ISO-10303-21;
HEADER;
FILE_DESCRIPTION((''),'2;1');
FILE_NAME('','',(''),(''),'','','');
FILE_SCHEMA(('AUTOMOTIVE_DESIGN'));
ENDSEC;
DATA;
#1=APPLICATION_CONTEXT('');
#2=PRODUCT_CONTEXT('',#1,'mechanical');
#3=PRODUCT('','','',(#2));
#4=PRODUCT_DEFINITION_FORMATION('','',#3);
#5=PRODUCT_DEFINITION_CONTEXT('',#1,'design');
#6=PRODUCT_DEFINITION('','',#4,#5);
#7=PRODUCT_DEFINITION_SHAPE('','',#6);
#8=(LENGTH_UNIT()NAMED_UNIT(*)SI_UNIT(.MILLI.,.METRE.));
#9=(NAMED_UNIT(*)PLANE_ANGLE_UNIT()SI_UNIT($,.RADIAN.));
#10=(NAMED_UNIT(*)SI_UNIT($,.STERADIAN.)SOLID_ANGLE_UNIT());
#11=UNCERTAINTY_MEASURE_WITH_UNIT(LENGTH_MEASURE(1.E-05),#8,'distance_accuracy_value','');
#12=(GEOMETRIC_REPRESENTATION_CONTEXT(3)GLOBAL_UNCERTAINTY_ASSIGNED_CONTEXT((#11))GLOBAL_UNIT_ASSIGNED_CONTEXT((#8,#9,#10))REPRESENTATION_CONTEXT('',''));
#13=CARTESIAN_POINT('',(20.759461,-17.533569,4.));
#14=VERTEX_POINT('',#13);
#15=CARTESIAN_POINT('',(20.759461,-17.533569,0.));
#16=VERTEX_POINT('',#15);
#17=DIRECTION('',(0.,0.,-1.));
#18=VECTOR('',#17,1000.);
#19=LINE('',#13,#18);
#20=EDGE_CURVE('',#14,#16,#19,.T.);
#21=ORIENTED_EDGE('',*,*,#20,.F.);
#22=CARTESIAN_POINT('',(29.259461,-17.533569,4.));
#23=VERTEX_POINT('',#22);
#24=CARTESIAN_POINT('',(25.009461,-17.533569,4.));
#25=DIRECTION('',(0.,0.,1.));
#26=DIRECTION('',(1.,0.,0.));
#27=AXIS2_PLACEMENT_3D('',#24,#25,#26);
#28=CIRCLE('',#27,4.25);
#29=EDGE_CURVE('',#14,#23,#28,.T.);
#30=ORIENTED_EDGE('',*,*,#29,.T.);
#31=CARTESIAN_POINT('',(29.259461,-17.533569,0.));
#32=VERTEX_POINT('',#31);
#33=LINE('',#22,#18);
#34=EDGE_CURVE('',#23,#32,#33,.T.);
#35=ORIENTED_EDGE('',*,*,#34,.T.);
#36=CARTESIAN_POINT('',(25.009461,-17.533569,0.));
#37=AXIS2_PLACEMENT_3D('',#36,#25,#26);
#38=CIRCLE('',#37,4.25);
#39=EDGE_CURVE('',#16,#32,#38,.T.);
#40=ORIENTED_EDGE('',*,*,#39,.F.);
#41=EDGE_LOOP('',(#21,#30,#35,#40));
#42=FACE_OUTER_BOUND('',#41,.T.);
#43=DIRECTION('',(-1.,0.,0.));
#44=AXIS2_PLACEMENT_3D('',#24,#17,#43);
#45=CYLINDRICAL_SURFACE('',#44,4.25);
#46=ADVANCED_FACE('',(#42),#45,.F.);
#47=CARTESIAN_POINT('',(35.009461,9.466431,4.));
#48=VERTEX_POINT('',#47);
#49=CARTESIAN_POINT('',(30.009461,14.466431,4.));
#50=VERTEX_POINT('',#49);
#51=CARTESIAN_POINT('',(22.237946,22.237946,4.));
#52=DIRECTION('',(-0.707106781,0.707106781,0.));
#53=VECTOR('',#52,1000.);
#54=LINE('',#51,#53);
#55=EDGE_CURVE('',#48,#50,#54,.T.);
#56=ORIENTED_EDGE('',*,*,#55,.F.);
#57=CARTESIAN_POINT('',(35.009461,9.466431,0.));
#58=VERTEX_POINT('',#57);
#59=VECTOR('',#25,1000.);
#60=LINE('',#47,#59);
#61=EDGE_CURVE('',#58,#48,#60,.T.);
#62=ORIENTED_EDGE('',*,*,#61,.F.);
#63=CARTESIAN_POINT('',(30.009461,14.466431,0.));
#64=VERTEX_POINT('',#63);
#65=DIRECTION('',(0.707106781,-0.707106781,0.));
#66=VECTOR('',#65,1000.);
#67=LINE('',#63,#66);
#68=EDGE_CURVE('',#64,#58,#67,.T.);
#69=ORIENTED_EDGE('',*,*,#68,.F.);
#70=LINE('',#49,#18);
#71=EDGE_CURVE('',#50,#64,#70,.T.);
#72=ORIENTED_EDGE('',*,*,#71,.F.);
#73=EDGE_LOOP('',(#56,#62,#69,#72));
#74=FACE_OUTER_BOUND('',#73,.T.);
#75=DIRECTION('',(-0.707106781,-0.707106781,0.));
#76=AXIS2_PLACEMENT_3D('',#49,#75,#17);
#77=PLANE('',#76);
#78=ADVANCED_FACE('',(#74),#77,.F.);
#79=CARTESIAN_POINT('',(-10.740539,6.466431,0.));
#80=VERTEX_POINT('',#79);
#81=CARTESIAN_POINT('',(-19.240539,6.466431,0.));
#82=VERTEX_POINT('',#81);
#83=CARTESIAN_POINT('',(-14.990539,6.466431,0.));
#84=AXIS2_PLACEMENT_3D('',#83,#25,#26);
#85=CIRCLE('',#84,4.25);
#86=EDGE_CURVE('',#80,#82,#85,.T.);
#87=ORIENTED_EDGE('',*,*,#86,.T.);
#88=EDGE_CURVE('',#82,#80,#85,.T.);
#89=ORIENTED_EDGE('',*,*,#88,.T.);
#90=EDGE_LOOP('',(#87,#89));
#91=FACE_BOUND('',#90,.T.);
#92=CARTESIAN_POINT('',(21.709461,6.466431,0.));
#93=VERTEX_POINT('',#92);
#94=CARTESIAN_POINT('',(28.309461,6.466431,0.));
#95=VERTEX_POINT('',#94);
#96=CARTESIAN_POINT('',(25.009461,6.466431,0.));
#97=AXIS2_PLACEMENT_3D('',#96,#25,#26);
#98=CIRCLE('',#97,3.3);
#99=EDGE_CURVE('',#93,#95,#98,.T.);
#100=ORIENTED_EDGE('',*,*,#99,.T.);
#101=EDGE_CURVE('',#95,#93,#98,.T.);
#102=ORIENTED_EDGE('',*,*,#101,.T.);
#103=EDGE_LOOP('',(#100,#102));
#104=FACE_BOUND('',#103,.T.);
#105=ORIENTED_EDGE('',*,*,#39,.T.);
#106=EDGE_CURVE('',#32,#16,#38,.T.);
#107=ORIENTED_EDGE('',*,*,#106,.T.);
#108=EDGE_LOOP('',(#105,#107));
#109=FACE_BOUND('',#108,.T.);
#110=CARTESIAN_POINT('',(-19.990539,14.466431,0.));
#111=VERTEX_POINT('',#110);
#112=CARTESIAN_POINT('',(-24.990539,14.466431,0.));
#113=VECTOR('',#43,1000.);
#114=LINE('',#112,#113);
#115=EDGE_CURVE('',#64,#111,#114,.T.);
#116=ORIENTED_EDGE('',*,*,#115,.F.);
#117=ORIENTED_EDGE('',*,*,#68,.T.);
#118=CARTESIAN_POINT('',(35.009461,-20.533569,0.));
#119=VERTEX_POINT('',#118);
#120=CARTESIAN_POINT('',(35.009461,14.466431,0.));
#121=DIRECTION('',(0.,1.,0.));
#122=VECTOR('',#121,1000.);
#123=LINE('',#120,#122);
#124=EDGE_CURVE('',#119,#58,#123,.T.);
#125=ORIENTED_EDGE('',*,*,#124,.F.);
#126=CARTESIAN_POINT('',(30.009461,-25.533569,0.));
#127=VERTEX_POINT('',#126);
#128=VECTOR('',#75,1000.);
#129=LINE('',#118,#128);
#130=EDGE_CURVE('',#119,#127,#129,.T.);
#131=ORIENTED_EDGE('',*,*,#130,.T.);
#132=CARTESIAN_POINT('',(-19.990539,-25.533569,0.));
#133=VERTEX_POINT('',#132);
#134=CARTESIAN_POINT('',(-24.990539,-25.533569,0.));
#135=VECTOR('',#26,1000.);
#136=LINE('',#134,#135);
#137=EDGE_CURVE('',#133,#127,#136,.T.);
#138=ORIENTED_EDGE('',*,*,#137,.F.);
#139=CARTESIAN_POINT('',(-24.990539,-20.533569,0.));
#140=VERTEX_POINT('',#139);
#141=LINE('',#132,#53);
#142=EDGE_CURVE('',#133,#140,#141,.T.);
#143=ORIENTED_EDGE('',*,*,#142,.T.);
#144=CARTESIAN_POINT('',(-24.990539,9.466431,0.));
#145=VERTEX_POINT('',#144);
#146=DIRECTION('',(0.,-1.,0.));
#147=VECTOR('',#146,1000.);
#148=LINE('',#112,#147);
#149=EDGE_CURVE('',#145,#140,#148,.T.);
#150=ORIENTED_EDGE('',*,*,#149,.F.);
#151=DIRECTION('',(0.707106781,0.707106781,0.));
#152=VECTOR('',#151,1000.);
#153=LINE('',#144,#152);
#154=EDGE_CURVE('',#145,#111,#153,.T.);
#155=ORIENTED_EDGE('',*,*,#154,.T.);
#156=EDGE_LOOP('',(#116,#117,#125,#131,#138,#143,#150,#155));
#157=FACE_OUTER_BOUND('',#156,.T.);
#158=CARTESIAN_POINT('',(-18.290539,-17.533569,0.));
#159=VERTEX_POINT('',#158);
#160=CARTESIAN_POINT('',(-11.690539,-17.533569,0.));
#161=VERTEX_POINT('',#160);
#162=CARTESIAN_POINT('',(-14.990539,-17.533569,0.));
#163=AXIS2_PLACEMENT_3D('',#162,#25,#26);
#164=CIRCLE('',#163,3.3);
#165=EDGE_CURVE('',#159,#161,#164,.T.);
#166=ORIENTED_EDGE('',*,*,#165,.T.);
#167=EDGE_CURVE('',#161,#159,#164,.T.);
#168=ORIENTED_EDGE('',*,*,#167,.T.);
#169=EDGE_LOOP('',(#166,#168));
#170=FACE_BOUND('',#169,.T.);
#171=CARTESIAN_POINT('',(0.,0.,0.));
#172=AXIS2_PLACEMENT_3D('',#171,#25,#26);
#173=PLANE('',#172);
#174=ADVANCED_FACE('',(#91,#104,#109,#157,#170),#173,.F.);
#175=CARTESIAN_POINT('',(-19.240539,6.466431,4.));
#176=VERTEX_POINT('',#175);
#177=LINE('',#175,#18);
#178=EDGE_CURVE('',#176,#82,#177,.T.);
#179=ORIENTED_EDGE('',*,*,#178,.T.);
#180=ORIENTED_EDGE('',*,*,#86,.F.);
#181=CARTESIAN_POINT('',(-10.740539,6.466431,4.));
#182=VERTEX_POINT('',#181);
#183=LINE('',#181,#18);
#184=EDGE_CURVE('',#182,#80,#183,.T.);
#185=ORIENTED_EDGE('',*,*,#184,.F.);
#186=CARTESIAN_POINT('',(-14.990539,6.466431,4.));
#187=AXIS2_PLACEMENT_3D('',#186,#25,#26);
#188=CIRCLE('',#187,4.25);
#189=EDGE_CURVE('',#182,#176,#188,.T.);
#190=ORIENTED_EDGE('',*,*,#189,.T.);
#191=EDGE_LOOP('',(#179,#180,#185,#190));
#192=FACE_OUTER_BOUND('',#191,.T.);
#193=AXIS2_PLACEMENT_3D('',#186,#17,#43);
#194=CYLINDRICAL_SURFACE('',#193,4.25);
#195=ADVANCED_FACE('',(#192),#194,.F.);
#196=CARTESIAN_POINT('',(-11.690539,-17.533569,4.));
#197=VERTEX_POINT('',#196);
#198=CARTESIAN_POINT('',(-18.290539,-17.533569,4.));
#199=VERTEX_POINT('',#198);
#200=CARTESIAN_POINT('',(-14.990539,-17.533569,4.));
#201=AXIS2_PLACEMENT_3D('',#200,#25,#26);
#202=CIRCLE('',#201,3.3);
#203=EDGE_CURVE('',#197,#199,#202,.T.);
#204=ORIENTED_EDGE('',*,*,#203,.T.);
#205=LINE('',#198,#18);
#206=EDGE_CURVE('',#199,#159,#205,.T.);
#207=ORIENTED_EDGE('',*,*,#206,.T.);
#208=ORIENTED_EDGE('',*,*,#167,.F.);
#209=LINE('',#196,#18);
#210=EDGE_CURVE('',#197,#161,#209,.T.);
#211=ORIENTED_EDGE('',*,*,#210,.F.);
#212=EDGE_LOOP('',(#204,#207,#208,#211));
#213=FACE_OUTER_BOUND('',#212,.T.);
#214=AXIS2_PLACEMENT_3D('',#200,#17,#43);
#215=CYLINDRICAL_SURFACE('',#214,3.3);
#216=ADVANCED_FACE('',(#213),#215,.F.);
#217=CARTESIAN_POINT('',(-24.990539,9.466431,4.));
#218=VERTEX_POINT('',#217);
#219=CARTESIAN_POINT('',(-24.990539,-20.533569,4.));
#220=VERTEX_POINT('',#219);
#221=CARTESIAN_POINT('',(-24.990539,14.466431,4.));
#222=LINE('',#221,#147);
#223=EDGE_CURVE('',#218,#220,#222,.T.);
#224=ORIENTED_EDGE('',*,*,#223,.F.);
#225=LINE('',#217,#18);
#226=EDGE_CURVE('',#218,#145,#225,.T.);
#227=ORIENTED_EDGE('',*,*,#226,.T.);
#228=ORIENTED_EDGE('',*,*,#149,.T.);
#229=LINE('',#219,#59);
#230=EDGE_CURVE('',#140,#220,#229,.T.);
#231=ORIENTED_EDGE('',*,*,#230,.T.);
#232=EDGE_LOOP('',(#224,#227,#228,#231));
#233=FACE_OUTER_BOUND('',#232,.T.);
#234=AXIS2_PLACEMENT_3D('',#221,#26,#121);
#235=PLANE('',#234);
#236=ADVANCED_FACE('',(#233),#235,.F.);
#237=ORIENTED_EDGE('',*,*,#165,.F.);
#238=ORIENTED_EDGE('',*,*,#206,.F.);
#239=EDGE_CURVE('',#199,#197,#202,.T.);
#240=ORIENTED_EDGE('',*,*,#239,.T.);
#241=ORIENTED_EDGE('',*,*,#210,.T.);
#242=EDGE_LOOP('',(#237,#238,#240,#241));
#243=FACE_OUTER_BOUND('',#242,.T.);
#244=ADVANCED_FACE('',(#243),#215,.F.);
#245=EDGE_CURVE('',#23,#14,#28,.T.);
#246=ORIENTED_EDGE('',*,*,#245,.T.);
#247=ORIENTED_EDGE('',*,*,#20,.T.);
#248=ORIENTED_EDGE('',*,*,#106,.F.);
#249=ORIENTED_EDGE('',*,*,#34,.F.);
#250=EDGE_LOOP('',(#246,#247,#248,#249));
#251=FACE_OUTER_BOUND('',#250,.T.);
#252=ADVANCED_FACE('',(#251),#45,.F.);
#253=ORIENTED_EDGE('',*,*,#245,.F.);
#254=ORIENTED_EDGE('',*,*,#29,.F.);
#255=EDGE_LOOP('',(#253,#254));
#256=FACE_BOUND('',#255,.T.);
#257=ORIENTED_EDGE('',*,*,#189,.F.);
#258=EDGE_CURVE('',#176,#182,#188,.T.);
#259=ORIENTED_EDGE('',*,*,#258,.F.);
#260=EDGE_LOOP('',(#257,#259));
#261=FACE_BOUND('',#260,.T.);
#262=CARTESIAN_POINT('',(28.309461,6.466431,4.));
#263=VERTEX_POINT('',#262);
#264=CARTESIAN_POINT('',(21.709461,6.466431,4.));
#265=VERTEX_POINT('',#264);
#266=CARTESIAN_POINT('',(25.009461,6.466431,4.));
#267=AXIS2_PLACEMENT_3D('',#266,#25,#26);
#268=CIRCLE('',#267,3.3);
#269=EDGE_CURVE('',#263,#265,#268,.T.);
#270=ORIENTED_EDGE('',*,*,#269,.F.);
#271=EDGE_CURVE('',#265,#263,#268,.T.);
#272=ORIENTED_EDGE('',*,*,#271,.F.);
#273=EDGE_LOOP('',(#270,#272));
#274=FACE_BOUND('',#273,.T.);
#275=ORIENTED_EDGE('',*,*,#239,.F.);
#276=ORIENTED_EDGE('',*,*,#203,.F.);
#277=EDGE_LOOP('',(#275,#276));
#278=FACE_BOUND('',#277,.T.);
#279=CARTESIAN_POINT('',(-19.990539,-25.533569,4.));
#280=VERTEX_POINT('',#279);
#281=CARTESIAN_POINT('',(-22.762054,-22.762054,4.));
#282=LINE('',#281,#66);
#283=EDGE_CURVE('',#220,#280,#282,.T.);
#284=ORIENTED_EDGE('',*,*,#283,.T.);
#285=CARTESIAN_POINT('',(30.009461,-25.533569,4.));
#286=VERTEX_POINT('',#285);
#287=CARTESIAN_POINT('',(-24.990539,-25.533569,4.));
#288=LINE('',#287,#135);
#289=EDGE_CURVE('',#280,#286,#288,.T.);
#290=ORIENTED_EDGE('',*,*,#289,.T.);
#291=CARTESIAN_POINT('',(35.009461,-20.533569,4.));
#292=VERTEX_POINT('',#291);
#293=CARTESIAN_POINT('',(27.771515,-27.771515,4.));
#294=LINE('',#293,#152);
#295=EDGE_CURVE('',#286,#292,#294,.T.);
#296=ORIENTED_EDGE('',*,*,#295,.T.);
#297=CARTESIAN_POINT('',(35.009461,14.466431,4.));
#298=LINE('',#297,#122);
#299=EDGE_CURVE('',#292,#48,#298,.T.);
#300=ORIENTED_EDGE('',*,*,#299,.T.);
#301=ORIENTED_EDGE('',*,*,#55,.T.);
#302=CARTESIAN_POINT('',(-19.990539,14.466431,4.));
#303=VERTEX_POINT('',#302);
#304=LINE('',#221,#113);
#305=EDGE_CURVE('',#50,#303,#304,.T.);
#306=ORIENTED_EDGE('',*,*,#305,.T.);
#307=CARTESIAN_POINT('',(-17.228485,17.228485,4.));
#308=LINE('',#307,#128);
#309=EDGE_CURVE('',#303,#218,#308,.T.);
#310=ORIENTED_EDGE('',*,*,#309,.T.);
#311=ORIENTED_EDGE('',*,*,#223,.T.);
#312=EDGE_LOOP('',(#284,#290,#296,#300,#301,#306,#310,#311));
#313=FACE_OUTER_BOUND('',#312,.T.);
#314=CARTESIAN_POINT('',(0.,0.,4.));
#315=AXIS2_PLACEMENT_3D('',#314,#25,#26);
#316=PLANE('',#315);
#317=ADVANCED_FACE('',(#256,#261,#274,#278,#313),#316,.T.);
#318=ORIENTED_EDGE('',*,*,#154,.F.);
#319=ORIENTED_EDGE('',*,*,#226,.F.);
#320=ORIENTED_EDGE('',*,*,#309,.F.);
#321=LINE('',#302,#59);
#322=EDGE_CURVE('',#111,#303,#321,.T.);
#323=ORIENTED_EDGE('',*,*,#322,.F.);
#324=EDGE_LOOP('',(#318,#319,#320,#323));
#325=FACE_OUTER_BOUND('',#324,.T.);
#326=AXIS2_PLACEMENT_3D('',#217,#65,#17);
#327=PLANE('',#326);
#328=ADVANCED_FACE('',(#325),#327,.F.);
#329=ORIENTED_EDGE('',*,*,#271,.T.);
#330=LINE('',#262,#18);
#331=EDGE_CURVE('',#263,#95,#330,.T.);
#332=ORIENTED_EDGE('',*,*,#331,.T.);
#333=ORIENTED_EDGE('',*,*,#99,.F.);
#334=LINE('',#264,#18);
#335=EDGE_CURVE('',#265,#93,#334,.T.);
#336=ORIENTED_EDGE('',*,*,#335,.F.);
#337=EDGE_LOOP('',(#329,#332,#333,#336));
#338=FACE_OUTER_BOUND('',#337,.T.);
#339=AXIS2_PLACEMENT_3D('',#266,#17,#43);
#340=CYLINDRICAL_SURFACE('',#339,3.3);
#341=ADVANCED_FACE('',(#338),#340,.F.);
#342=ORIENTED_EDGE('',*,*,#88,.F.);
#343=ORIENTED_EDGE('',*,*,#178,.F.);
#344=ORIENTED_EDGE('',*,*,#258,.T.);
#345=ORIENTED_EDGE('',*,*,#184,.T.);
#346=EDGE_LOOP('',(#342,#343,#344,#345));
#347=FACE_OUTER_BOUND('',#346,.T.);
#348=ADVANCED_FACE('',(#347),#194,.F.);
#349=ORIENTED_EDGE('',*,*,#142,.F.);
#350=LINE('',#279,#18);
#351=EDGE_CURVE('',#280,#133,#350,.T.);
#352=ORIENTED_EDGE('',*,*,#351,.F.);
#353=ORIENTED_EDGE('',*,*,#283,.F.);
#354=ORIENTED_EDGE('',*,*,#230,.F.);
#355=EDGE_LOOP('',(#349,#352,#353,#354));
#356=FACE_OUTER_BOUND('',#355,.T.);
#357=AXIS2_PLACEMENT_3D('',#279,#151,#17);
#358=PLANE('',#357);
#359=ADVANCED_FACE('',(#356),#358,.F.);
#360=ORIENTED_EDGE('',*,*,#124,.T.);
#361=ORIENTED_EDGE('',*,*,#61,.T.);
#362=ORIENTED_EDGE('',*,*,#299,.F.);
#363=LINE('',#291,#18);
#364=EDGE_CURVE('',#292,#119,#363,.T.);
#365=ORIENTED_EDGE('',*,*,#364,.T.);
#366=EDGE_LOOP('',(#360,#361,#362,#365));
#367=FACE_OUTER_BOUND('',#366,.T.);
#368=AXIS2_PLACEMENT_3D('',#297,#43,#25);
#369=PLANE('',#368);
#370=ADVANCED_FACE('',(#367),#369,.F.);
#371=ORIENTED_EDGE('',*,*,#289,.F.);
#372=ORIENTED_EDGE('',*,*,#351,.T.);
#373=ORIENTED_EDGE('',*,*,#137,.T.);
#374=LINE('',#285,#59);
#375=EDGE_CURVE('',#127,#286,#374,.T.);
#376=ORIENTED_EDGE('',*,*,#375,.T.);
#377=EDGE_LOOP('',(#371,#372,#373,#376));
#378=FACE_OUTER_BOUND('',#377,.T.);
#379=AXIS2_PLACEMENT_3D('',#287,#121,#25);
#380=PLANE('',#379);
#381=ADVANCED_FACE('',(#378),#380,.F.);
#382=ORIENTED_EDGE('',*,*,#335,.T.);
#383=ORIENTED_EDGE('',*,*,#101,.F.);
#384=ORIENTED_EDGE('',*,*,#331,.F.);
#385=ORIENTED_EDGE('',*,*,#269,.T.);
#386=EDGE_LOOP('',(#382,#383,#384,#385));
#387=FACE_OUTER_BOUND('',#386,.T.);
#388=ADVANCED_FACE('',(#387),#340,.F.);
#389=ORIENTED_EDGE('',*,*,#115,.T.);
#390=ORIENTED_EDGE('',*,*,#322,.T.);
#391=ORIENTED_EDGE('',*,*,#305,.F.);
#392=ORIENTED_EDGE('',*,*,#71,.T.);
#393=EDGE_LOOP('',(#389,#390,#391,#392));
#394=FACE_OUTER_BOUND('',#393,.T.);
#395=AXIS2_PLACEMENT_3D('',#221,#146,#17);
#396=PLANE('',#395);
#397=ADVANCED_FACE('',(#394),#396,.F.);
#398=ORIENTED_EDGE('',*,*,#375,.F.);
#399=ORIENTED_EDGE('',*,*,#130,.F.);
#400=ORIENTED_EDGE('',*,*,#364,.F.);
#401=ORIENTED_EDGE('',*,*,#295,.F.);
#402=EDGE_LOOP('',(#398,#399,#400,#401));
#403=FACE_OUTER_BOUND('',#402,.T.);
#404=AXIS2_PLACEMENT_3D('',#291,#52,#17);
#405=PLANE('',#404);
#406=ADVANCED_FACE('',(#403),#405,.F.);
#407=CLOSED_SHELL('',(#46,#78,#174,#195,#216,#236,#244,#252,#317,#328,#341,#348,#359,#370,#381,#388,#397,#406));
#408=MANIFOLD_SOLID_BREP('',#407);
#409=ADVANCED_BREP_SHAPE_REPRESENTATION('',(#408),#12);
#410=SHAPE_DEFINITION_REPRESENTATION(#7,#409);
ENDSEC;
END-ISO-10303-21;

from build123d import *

# Parameters (mm, degrees)
SKETCH1_W           = 60
SKETCH1_H           = 40
SKETCH1_R           = 4.25
SKETCH1_R_2         = 3.3
BOSS_EXTRUDE1_DEPTH = 4
CHAMFER1_SIZE       = 5


with BuildPart() as part:
    # Sketch1 → Boss-Extrude1 (new body)
    with BuildSketch(Plane.XY):
        with Locations((5.009460805, -5.533568905)):
            Rectangle(SKETCH1_W, SKETCH1_H)
        with Locations((-14.990539195, 6.466431095)):
            Circle(SKETCH1_R, mode=Mode.SUBTRACT)
        with Locations((25.009460805, -17.533568905)):
            Circle(SKETCH1_R, mode=Mode.SUBTRACT)
        with Locations((25.009460805, 6.466431095)):
            Circle(SKETCH1_R_2, mode=Mode.SUBTRACT)
        with Locations((-14.990539195, -17.533568905)):
            Circle(SKETCH1_R_2, mode=Mode.SUBTRACT)
    extrude(amount=BOSS_EXTRUDE1_DEPTH)

    # Chamfer1
    chamfer1_edges = [part.edges().sort_by_distance(p)[0] for p in [
        (-24.990539195, 14.466431095, 2),
        (35.009460805, 14.466431095, 2),
        (35.009460805, -25.533568905, 2),
        (-24.990539195, -25.533568905, 2),
    ]]
    chamfer(chamfer1_edges, length=CHAMFER1_SIZE)


solid = part.part
